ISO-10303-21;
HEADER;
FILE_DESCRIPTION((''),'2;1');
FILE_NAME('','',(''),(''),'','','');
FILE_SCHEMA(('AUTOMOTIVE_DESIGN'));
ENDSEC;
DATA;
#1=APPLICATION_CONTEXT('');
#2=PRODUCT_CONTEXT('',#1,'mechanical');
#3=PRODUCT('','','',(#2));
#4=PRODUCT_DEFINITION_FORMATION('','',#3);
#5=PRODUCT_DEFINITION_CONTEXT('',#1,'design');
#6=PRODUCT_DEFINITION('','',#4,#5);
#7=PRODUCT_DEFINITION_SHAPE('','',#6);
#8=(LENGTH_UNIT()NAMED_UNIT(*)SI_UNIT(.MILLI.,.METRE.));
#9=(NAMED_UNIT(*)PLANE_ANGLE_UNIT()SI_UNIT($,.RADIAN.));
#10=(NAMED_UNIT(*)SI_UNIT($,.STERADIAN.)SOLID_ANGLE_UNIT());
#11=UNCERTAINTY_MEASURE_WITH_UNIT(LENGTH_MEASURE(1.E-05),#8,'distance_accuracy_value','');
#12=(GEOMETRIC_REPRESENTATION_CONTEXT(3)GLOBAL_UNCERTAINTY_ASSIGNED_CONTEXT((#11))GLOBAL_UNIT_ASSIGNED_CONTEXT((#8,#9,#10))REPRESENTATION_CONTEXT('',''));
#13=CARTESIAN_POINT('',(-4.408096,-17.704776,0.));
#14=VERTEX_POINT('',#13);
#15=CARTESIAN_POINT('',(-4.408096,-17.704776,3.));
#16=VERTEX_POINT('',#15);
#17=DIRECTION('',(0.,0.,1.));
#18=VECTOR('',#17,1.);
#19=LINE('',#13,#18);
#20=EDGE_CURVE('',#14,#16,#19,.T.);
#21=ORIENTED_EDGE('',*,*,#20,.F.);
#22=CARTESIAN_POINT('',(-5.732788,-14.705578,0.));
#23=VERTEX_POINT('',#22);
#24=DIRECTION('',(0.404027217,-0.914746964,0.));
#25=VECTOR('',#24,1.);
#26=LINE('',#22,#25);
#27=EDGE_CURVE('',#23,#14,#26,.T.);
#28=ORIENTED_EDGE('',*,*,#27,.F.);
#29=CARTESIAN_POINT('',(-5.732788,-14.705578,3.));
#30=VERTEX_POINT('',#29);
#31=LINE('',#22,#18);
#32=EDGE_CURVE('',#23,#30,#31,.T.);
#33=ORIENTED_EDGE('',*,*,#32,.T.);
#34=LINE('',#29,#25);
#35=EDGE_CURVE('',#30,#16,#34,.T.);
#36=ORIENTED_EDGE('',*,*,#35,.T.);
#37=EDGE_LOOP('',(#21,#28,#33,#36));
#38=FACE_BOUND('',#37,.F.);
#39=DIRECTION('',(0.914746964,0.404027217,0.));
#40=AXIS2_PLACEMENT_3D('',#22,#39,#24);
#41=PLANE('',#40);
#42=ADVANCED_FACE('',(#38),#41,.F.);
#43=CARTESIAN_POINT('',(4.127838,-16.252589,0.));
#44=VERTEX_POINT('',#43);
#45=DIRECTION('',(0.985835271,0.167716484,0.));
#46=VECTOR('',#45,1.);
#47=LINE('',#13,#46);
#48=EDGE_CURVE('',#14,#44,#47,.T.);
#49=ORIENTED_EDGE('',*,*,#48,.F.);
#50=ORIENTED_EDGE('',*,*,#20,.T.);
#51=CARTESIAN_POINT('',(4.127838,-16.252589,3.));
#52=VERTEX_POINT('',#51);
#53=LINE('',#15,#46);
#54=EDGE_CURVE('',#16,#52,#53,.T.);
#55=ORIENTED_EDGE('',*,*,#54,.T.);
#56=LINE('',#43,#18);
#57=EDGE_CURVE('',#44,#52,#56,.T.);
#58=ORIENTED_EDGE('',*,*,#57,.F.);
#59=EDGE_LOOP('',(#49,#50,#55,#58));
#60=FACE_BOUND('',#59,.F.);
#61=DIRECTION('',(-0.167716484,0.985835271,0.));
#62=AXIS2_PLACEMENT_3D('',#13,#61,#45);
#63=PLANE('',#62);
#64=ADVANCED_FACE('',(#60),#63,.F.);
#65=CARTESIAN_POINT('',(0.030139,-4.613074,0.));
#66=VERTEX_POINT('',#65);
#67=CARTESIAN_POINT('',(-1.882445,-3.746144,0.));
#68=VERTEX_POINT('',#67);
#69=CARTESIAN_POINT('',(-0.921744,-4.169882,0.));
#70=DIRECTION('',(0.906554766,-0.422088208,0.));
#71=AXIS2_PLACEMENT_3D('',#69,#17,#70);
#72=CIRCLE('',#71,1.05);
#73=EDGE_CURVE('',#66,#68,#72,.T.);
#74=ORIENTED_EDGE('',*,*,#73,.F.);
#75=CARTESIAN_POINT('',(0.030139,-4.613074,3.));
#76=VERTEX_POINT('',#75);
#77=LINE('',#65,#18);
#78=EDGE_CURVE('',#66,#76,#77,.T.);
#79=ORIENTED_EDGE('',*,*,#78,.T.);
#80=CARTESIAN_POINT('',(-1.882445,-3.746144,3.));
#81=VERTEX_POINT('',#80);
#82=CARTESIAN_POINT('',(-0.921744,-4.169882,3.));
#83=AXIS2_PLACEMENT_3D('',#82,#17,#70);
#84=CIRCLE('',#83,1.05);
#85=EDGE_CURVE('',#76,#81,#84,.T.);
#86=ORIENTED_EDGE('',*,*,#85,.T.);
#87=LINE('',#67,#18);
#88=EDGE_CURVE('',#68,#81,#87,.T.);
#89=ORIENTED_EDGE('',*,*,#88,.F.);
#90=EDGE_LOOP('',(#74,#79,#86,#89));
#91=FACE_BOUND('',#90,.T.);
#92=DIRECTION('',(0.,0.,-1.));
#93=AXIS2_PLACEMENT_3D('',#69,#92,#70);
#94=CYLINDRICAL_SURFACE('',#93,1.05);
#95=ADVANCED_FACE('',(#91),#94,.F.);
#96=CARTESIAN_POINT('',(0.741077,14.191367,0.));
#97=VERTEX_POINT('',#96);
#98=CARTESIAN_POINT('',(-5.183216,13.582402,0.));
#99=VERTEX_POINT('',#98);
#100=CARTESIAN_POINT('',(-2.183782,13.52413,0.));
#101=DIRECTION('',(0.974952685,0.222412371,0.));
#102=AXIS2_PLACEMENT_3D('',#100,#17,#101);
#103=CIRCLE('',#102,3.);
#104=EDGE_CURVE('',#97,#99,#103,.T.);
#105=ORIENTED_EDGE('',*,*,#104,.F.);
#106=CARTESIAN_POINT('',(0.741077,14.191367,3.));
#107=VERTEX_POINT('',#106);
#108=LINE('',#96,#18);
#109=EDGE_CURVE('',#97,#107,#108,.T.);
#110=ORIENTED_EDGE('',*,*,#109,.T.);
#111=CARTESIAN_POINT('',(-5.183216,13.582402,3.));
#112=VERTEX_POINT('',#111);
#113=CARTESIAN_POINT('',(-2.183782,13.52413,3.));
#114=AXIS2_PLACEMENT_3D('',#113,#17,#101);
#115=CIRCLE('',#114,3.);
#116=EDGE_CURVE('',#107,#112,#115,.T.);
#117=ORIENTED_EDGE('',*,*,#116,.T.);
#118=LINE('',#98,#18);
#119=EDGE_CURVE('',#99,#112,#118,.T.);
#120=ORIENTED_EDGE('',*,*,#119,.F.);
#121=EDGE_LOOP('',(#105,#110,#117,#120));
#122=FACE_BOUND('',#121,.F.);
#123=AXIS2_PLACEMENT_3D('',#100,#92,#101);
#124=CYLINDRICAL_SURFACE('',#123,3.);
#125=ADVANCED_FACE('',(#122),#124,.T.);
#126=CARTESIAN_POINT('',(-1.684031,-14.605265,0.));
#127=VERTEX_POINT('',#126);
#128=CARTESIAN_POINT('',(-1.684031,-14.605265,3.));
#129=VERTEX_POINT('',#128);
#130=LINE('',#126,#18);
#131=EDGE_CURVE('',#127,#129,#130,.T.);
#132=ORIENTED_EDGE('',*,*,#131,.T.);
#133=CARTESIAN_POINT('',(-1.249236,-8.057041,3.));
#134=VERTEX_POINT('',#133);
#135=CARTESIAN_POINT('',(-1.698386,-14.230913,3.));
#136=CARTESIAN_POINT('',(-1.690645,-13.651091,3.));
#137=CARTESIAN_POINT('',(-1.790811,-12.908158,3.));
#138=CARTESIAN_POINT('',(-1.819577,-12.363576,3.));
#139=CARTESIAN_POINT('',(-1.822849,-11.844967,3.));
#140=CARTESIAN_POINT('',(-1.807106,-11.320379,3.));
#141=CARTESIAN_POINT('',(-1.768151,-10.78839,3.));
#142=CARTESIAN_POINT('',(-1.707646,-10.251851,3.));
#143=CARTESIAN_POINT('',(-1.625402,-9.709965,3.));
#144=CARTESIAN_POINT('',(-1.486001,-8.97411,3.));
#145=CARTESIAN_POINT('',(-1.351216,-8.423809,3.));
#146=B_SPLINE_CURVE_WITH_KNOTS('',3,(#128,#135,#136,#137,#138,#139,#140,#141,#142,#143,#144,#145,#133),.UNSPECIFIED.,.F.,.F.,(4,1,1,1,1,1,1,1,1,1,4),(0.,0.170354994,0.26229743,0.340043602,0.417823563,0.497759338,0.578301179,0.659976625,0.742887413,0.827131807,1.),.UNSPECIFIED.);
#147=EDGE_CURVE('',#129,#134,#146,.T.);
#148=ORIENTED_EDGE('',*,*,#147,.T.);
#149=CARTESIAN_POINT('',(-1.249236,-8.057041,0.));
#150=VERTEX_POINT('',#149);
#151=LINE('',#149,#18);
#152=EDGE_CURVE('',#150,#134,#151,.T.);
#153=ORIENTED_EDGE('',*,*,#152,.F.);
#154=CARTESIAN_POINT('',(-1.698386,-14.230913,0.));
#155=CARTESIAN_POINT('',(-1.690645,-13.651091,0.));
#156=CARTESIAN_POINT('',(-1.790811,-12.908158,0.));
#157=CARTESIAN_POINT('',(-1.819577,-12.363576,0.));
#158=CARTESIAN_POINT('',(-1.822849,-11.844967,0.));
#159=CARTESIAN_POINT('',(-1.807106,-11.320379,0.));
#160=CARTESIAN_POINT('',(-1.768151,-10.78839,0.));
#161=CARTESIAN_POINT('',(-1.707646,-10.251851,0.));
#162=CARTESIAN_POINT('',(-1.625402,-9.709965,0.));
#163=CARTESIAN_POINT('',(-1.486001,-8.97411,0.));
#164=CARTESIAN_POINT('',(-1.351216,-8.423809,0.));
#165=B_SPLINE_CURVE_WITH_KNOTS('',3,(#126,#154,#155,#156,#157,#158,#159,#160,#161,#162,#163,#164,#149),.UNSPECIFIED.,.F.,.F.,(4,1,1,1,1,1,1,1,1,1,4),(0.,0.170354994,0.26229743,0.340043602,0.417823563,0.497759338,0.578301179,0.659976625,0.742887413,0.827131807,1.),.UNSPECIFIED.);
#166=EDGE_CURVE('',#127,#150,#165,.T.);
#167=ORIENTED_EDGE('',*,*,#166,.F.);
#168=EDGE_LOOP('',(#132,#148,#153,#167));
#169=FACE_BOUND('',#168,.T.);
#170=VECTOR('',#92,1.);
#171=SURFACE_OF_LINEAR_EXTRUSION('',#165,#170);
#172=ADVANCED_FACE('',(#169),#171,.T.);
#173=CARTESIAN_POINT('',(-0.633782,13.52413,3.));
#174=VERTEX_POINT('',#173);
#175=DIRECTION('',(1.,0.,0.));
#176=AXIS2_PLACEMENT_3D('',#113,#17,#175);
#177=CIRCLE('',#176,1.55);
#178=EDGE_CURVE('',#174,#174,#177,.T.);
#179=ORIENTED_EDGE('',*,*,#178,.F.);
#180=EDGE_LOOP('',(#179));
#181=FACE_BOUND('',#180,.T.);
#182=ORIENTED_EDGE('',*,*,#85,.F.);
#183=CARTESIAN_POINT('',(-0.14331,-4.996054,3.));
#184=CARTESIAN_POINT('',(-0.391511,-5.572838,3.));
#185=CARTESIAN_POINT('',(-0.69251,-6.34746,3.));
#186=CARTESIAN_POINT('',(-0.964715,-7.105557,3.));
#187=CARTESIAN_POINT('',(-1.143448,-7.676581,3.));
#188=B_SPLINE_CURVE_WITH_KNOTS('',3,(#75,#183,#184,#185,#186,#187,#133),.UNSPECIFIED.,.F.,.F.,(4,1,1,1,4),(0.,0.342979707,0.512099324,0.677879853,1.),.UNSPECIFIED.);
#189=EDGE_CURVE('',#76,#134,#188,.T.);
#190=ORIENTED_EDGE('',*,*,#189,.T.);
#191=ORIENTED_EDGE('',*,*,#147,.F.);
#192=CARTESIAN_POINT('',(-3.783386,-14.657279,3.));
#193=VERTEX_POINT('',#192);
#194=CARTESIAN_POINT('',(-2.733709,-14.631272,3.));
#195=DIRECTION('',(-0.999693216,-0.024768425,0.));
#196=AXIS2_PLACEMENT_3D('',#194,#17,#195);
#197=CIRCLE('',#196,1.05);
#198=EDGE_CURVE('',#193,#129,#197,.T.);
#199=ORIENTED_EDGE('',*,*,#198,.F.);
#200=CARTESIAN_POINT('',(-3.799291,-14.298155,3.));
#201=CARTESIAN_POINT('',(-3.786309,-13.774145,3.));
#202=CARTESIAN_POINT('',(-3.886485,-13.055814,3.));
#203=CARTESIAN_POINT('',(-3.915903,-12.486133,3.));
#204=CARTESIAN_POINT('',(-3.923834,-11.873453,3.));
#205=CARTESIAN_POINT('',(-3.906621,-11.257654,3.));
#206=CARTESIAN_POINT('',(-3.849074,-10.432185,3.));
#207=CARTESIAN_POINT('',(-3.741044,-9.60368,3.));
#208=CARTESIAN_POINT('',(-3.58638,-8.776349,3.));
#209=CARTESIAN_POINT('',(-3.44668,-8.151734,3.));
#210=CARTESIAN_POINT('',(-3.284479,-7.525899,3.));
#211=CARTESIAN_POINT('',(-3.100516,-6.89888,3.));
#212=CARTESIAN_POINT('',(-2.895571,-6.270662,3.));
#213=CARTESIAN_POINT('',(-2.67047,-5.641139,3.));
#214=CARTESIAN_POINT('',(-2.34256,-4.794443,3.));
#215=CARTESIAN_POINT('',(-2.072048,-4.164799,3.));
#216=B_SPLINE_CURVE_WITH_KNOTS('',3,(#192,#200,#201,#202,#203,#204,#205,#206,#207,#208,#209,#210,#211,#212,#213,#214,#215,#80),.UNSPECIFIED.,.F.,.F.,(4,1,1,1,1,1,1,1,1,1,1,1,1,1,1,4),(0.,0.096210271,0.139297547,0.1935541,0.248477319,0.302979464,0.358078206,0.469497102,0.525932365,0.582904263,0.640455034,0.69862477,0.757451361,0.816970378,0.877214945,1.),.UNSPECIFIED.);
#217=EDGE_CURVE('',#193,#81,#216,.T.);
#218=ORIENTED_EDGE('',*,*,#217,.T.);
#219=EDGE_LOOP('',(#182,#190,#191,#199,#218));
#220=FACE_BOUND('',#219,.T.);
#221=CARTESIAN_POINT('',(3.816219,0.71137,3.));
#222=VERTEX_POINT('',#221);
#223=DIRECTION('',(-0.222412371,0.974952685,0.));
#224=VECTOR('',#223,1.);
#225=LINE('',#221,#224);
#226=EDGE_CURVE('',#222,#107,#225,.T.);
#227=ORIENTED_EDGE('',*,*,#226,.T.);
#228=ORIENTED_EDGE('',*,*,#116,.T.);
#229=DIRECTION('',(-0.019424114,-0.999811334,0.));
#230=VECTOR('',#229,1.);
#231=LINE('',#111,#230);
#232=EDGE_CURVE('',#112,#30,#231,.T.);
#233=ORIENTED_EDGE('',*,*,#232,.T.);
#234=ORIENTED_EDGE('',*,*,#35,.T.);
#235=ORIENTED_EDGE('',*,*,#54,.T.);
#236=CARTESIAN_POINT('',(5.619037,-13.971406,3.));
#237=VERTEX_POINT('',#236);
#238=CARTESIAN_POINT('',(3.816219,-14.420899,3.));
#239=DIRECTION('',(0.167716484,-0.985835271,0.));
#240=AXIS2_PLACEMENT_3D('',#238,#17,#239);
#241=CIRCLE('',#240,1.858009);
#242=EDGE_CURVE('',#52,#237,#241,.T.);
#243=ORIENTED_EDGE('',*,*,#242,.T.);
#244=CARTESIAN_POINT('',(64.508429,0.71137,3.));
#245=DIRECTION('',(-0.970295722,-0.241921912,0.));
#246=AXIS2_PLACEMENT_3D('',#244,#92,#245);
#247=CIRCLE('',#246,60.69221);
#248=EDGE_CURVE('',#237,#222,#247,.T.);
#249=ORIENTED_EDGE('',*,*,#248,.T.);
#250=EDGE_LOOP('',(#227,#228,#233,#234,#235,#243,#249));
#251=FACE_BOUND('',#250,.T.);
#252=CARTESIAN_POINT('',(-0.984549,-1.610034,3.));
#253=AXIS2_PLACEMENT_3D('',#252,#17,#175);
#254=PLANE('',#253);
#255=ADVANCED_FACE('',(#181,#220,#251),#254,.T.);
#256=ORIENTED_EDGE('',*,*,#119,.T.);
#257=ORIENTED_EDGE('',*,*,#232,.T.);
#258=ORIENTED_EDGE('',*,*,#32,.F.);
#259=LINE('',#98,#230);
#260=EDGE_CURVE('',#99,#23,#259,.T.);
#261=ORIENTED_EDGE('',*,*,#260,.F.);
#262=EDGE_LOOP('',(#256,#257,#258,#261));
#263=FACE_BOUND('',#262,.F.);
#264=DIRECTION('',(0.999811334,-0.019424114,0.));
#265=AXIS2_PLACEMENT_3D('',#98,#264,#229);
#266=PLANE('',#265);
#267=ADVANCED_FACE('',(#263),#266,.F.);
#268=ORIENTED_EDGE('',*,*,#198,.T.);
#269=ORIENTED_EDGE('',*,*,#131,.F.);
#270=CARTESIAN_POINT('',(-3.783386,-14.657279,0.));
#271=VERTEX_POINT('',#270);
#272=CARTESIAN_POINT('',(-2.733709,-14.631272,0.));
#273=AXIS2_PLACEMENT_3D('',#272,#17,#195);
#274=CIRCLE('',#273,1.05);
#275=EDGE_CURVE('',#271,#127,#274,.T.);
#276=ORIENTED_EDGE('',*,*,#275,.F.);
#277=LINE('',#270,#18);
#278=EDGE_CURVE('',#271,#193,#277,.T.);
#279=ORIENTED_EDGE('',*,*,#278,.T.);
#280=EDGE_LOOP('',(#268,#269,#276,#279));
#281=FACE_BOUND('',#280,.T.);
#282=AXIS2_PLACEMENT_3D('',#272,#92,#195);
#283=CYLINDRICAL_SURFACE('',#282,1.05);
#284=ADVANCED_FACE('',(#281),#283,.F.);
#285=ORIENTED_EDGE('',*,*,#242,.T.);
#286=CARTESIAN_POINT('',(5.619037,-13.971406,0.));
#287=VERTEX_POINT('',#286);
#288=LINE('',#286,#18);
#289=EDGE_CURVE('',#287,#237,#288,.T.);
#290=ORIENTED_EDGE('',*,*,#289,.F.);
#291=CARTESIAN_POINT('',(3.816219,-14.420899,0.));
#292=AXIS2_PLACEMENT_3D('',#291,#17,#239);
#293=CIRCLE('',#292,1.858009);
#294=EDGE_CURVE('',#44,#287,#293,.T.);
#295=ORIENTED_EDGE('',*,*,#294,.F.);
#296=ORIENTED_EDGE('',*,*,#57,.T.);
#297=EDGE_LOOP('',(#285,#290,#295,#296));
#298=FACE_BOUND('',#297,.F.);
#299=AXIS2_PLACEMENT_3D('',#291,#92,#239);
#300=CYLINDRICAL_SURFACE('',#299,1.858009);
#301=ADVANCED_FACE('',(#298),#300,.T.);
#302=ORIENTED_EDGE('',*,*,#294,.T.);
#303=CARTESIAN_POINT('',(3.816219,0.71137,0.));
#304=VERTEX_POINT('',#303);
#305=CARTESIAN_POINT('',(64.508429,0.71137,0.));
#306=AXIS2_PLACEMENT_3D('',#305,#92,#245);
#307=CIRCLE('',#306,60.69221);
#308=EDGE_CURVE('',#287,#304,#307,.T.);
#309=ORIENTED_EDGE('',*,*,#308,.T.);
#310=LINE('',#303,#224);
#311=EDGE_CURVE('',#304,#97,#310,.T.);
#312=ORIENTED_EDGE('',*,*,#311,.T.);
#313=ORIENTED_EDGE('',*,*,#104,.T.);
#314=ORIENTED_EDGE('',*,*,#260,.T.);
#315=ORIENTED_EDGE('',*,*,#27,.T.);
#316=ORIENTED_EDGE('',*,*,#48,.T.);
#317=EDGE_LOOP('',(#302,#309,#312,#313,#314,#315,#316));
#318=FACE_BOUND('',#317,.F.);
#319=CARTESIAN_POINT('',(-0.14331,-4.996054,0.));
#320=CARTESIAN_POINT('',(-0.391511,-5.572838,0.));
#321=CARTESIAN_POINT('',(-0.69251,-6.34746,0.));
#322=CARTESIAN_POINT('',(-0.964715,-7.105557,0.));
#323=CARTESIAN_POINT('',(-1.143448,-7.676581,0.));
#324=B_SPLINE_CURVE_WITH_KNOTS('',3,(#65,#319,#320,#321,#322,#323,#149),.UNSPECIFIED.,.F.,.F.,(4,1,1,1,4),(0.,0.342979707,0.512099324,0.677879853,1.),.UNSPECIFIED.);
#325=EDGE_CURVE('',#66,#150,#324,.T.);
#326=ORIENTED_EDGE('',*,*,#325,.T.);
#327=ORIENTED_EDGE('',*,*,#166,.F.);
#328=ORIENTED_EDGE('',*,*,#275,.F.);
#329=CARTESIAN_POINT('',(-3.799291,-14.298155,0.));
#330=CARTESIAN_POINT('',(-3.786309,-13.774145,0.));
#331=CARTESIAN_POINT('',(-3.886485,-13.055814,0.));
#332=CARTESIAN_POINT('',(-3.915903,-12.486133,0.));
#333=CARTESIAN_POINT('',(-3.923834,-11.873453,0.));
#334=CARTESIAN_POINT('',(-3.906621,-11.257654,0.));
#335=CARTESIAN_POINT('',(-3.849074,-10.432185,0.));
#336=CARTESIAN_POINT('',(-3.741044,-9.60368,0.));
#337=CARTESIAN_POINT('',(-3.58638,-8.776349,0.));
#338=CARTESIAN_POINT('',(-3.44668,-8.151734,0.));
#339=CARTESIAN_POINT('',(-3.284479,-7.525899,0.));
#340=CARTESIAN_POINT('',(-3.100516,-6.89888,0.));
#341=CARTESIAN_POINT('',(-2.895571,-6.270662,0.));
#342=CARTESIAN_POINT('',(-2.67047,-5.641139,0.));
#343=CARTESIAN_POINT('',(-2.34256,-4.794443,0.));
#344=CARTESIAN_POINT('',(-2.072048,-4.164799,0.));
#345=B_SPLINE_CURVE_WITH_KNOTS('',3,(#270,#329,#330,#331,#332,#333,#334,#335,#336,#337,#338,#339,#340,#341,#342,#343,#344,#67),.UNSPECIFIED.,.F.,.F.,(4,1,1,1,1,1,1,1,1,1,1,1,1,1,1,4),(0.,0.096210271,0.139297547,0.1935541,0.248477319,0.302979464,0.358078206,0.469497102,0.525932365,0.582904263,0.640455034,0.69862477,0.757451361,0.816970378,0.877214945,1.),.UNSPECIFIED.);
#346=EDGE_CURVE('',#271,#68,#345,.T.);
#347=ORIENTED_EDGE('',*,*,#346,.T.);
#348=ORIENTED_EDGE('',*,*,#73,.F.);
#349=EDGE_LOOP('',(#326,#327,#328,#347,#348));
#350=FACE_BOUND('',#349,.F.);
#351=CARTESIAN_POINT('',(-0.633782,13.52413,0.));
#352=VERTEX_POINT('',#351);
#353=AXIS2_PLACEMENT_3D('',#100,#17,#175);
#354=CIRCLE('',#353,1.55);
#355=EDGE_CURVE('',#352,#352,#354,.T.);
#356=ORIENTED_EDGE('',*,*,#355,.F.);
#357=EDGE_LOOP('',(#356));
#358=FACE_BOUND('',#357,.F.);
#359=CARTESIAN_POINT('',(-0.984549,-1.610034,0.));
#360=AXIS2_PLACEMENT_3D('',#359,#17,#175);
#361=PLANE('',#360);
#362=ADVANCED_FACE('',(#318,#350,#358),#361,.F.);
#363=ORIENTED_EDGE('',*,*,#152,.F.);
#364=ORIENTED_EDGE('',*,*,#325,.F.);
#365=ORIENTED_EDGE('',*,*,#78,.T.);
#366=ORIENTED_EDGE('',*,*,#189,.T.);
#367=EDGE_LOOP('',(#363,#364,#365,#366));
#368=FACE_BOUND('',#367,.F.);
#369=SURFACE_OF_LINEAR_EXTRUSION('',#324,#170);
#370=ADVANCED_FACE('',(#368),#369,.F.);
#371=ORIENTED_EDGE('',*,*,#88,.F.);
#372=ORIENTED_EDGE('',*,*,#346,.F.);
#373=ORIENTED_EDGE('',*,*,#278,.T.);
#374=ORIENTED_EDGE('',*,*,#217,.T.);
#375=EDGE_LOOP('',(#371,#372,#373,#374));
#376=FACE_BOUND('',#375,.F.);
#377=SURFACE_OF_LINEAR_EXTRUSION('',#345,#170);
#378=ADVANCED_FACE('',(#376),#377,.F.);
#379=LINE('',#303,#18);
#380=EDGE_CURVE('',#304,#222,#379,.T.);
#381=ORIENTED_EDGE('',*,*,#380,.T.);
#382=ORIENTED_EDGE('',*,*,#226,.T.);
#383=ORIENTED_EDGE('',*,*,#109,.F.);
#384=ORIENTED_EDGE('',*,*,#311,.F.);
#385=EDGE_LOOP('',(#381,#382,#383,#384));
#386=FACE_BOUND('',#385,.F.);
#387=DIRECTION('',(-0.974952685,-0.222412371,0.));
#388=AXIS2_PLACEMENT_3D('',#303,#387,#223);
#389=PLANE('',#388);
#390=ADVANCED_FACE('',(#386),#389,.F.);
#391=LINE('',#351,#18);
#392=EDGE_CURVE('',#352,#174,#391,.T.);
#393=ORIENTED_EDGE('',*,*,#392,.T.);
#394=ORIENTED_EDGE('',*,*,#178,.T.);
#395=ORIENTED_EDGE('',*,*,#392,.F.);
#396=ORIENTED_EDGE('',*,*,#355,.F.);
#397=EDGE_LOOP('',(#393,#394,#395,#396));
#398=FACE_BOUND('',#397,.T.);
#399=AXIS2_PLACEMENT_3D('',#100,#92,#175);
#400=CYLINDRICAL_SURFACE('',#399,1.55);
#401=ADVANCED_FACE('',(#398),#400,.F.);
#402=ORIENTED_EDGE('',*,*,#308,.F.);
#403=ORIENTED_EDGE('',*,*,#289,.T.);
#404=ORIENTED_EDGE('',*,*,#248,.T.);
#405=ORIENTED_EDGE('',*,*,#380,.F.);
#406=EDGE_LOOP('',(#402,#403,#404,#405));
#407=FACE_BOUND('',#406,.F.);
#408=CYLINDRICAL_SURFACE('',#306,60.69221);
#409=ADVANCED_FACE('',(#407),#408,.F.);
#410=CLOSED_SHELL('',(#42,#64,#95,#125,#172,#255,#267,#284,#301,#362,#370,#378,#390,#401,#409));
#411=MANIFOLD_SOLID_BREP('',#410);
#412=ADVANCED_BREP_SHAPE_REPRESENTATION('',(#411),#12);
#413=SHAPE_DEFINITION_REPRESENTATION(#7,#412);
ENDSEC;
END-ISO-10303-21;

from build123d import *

# Parameters (mm, degrees)
SKETCH_1_R      = 1.55
EXTRUDE_1_DEPTH = 3


with BuildPart() as part:
    # 草图1 (on Front Plane) → 凸台-拉伸1 (new body)
    with BuildSketch(Plane.XY):
        with BuildLine():
            Line((3.816218697, 0.711369777), (0.741076539, 14.191366792))
            ThreePointArc((0.741076539, 14.191366792), (-2.49053861, 16.508405149), (-5.183215516, 13.582402021))
            Line((-5.183215516, 13.582402021), (-5.732788153, -14.705577537))
            Line((-5.732788153, -14.705577537), (-4.408096335, -17.704776028))
            Line((-4.408096335, -17.704776028), (4.127837654, -16.252589359))
            ThreePointArc((4.127837654, -16.252589359), (5.371423242, -15.437528643), (5.619036958, -13.971405684))
            ThreePointArc((5.619036958, -13.971405684), (4.268609288, -6.685150501), (3.816218697, 0.711369777))
        make_face()
        with Locations((-2.183781514, 13.524129678)):
            Circle(SKETCH_1_R, mode=Mode.SUBTRACT)
        with BuildLine():
            ThreePointArc((-3.783386383, -14.657279108), (-2.707701661, -15.680950138), (-1.684030631, -14.605265415))
            add(Edge.make_bspline(
                [(-1.684030631, -14.605265415), (-1.698385943, -14.230913496), (-1.690645088, -13.65109076), (-1.790811076, -12.90815818), (-1.819576713, -12.363575922), (-1.822848669, -11.844967012), (-1.807105928, -11.320378821), (-1.768151471, -10.788389789), (-1.707646295, -10.25185083), (-1.625402268, -9.709964922), (-1.486001031, -8.974109842), (-1.351215721, -8.423808693), (-1.249236023, -8.057041386)],
                knots=[0, 0, 0, 0, 0.170354994, 0.26229743, 0.340043602, 0.417823563, 0.497759338, 0.578301179, 0.659976625, 0.742887413, 0.827131807, 1, 1, 1, 1], degree=3))
            add(Edge.make_bspline(
                [(0.03013882, -4.613074169), (-0.143309735, -4.996054164), (-0.391510935, -5.572837816), (-0.692509933, -6.347460357), (-0.964714861, -7.105557392), (-1.143447826, -7.676581339), (-1.249236023, -8.057041386)],
                knots=[0, 0, 0, 0, 0.342979707, 0.512099324, 0.677879853, 1, 1, 1, 1], degree=3))
            ThreePointArc((0.03013882, -4.613074169), (-0.488256217, -3.213540285), (-1.882444762, -3.746144084))
            add(Edge.make_bspline(
                [(-3.783386383, -14.657279108), (-3.799290999, -14.2981548), (-3.786309002, -13.774144994), (-3.886484574, -13.055813522), (-3.915903208, -12.486133418), (-3.923833984, -11.87345296), (-3.906620769, -11.257653943), (-3.849073975, -10.432184554), (-3.741043656, -9.603680421), (-3.586380227, -8.77634916), (-3.446679883, -8.151733856), (-3.28447898, -7.525898679), (-3.10051603, -6.898880381), (-2.895571139, -6.270661953), (-2.670469593, -5.64113868), (-2.342560405, -4.794442901), (-2.072047563, -4.164799113), (-1.882444762, -3.746144084)],
                knots=[0, 0, 0, 0, 0.096210271, 0.139297547, 0.1935541, 0.248477319, 0.302979464, 0.358078206, 0.469497102, 0.525932365, 0.582904263, 0.640455034, 0.69862477, 0.757451361, 0.816970378, 0.877214945, 1, 1, 1, 1], degree=3))
        make_face(mode=Mode.SUBTRACT)
    extrude(amount=EXTRUDE_1_DEPTH)


solid = part.part
